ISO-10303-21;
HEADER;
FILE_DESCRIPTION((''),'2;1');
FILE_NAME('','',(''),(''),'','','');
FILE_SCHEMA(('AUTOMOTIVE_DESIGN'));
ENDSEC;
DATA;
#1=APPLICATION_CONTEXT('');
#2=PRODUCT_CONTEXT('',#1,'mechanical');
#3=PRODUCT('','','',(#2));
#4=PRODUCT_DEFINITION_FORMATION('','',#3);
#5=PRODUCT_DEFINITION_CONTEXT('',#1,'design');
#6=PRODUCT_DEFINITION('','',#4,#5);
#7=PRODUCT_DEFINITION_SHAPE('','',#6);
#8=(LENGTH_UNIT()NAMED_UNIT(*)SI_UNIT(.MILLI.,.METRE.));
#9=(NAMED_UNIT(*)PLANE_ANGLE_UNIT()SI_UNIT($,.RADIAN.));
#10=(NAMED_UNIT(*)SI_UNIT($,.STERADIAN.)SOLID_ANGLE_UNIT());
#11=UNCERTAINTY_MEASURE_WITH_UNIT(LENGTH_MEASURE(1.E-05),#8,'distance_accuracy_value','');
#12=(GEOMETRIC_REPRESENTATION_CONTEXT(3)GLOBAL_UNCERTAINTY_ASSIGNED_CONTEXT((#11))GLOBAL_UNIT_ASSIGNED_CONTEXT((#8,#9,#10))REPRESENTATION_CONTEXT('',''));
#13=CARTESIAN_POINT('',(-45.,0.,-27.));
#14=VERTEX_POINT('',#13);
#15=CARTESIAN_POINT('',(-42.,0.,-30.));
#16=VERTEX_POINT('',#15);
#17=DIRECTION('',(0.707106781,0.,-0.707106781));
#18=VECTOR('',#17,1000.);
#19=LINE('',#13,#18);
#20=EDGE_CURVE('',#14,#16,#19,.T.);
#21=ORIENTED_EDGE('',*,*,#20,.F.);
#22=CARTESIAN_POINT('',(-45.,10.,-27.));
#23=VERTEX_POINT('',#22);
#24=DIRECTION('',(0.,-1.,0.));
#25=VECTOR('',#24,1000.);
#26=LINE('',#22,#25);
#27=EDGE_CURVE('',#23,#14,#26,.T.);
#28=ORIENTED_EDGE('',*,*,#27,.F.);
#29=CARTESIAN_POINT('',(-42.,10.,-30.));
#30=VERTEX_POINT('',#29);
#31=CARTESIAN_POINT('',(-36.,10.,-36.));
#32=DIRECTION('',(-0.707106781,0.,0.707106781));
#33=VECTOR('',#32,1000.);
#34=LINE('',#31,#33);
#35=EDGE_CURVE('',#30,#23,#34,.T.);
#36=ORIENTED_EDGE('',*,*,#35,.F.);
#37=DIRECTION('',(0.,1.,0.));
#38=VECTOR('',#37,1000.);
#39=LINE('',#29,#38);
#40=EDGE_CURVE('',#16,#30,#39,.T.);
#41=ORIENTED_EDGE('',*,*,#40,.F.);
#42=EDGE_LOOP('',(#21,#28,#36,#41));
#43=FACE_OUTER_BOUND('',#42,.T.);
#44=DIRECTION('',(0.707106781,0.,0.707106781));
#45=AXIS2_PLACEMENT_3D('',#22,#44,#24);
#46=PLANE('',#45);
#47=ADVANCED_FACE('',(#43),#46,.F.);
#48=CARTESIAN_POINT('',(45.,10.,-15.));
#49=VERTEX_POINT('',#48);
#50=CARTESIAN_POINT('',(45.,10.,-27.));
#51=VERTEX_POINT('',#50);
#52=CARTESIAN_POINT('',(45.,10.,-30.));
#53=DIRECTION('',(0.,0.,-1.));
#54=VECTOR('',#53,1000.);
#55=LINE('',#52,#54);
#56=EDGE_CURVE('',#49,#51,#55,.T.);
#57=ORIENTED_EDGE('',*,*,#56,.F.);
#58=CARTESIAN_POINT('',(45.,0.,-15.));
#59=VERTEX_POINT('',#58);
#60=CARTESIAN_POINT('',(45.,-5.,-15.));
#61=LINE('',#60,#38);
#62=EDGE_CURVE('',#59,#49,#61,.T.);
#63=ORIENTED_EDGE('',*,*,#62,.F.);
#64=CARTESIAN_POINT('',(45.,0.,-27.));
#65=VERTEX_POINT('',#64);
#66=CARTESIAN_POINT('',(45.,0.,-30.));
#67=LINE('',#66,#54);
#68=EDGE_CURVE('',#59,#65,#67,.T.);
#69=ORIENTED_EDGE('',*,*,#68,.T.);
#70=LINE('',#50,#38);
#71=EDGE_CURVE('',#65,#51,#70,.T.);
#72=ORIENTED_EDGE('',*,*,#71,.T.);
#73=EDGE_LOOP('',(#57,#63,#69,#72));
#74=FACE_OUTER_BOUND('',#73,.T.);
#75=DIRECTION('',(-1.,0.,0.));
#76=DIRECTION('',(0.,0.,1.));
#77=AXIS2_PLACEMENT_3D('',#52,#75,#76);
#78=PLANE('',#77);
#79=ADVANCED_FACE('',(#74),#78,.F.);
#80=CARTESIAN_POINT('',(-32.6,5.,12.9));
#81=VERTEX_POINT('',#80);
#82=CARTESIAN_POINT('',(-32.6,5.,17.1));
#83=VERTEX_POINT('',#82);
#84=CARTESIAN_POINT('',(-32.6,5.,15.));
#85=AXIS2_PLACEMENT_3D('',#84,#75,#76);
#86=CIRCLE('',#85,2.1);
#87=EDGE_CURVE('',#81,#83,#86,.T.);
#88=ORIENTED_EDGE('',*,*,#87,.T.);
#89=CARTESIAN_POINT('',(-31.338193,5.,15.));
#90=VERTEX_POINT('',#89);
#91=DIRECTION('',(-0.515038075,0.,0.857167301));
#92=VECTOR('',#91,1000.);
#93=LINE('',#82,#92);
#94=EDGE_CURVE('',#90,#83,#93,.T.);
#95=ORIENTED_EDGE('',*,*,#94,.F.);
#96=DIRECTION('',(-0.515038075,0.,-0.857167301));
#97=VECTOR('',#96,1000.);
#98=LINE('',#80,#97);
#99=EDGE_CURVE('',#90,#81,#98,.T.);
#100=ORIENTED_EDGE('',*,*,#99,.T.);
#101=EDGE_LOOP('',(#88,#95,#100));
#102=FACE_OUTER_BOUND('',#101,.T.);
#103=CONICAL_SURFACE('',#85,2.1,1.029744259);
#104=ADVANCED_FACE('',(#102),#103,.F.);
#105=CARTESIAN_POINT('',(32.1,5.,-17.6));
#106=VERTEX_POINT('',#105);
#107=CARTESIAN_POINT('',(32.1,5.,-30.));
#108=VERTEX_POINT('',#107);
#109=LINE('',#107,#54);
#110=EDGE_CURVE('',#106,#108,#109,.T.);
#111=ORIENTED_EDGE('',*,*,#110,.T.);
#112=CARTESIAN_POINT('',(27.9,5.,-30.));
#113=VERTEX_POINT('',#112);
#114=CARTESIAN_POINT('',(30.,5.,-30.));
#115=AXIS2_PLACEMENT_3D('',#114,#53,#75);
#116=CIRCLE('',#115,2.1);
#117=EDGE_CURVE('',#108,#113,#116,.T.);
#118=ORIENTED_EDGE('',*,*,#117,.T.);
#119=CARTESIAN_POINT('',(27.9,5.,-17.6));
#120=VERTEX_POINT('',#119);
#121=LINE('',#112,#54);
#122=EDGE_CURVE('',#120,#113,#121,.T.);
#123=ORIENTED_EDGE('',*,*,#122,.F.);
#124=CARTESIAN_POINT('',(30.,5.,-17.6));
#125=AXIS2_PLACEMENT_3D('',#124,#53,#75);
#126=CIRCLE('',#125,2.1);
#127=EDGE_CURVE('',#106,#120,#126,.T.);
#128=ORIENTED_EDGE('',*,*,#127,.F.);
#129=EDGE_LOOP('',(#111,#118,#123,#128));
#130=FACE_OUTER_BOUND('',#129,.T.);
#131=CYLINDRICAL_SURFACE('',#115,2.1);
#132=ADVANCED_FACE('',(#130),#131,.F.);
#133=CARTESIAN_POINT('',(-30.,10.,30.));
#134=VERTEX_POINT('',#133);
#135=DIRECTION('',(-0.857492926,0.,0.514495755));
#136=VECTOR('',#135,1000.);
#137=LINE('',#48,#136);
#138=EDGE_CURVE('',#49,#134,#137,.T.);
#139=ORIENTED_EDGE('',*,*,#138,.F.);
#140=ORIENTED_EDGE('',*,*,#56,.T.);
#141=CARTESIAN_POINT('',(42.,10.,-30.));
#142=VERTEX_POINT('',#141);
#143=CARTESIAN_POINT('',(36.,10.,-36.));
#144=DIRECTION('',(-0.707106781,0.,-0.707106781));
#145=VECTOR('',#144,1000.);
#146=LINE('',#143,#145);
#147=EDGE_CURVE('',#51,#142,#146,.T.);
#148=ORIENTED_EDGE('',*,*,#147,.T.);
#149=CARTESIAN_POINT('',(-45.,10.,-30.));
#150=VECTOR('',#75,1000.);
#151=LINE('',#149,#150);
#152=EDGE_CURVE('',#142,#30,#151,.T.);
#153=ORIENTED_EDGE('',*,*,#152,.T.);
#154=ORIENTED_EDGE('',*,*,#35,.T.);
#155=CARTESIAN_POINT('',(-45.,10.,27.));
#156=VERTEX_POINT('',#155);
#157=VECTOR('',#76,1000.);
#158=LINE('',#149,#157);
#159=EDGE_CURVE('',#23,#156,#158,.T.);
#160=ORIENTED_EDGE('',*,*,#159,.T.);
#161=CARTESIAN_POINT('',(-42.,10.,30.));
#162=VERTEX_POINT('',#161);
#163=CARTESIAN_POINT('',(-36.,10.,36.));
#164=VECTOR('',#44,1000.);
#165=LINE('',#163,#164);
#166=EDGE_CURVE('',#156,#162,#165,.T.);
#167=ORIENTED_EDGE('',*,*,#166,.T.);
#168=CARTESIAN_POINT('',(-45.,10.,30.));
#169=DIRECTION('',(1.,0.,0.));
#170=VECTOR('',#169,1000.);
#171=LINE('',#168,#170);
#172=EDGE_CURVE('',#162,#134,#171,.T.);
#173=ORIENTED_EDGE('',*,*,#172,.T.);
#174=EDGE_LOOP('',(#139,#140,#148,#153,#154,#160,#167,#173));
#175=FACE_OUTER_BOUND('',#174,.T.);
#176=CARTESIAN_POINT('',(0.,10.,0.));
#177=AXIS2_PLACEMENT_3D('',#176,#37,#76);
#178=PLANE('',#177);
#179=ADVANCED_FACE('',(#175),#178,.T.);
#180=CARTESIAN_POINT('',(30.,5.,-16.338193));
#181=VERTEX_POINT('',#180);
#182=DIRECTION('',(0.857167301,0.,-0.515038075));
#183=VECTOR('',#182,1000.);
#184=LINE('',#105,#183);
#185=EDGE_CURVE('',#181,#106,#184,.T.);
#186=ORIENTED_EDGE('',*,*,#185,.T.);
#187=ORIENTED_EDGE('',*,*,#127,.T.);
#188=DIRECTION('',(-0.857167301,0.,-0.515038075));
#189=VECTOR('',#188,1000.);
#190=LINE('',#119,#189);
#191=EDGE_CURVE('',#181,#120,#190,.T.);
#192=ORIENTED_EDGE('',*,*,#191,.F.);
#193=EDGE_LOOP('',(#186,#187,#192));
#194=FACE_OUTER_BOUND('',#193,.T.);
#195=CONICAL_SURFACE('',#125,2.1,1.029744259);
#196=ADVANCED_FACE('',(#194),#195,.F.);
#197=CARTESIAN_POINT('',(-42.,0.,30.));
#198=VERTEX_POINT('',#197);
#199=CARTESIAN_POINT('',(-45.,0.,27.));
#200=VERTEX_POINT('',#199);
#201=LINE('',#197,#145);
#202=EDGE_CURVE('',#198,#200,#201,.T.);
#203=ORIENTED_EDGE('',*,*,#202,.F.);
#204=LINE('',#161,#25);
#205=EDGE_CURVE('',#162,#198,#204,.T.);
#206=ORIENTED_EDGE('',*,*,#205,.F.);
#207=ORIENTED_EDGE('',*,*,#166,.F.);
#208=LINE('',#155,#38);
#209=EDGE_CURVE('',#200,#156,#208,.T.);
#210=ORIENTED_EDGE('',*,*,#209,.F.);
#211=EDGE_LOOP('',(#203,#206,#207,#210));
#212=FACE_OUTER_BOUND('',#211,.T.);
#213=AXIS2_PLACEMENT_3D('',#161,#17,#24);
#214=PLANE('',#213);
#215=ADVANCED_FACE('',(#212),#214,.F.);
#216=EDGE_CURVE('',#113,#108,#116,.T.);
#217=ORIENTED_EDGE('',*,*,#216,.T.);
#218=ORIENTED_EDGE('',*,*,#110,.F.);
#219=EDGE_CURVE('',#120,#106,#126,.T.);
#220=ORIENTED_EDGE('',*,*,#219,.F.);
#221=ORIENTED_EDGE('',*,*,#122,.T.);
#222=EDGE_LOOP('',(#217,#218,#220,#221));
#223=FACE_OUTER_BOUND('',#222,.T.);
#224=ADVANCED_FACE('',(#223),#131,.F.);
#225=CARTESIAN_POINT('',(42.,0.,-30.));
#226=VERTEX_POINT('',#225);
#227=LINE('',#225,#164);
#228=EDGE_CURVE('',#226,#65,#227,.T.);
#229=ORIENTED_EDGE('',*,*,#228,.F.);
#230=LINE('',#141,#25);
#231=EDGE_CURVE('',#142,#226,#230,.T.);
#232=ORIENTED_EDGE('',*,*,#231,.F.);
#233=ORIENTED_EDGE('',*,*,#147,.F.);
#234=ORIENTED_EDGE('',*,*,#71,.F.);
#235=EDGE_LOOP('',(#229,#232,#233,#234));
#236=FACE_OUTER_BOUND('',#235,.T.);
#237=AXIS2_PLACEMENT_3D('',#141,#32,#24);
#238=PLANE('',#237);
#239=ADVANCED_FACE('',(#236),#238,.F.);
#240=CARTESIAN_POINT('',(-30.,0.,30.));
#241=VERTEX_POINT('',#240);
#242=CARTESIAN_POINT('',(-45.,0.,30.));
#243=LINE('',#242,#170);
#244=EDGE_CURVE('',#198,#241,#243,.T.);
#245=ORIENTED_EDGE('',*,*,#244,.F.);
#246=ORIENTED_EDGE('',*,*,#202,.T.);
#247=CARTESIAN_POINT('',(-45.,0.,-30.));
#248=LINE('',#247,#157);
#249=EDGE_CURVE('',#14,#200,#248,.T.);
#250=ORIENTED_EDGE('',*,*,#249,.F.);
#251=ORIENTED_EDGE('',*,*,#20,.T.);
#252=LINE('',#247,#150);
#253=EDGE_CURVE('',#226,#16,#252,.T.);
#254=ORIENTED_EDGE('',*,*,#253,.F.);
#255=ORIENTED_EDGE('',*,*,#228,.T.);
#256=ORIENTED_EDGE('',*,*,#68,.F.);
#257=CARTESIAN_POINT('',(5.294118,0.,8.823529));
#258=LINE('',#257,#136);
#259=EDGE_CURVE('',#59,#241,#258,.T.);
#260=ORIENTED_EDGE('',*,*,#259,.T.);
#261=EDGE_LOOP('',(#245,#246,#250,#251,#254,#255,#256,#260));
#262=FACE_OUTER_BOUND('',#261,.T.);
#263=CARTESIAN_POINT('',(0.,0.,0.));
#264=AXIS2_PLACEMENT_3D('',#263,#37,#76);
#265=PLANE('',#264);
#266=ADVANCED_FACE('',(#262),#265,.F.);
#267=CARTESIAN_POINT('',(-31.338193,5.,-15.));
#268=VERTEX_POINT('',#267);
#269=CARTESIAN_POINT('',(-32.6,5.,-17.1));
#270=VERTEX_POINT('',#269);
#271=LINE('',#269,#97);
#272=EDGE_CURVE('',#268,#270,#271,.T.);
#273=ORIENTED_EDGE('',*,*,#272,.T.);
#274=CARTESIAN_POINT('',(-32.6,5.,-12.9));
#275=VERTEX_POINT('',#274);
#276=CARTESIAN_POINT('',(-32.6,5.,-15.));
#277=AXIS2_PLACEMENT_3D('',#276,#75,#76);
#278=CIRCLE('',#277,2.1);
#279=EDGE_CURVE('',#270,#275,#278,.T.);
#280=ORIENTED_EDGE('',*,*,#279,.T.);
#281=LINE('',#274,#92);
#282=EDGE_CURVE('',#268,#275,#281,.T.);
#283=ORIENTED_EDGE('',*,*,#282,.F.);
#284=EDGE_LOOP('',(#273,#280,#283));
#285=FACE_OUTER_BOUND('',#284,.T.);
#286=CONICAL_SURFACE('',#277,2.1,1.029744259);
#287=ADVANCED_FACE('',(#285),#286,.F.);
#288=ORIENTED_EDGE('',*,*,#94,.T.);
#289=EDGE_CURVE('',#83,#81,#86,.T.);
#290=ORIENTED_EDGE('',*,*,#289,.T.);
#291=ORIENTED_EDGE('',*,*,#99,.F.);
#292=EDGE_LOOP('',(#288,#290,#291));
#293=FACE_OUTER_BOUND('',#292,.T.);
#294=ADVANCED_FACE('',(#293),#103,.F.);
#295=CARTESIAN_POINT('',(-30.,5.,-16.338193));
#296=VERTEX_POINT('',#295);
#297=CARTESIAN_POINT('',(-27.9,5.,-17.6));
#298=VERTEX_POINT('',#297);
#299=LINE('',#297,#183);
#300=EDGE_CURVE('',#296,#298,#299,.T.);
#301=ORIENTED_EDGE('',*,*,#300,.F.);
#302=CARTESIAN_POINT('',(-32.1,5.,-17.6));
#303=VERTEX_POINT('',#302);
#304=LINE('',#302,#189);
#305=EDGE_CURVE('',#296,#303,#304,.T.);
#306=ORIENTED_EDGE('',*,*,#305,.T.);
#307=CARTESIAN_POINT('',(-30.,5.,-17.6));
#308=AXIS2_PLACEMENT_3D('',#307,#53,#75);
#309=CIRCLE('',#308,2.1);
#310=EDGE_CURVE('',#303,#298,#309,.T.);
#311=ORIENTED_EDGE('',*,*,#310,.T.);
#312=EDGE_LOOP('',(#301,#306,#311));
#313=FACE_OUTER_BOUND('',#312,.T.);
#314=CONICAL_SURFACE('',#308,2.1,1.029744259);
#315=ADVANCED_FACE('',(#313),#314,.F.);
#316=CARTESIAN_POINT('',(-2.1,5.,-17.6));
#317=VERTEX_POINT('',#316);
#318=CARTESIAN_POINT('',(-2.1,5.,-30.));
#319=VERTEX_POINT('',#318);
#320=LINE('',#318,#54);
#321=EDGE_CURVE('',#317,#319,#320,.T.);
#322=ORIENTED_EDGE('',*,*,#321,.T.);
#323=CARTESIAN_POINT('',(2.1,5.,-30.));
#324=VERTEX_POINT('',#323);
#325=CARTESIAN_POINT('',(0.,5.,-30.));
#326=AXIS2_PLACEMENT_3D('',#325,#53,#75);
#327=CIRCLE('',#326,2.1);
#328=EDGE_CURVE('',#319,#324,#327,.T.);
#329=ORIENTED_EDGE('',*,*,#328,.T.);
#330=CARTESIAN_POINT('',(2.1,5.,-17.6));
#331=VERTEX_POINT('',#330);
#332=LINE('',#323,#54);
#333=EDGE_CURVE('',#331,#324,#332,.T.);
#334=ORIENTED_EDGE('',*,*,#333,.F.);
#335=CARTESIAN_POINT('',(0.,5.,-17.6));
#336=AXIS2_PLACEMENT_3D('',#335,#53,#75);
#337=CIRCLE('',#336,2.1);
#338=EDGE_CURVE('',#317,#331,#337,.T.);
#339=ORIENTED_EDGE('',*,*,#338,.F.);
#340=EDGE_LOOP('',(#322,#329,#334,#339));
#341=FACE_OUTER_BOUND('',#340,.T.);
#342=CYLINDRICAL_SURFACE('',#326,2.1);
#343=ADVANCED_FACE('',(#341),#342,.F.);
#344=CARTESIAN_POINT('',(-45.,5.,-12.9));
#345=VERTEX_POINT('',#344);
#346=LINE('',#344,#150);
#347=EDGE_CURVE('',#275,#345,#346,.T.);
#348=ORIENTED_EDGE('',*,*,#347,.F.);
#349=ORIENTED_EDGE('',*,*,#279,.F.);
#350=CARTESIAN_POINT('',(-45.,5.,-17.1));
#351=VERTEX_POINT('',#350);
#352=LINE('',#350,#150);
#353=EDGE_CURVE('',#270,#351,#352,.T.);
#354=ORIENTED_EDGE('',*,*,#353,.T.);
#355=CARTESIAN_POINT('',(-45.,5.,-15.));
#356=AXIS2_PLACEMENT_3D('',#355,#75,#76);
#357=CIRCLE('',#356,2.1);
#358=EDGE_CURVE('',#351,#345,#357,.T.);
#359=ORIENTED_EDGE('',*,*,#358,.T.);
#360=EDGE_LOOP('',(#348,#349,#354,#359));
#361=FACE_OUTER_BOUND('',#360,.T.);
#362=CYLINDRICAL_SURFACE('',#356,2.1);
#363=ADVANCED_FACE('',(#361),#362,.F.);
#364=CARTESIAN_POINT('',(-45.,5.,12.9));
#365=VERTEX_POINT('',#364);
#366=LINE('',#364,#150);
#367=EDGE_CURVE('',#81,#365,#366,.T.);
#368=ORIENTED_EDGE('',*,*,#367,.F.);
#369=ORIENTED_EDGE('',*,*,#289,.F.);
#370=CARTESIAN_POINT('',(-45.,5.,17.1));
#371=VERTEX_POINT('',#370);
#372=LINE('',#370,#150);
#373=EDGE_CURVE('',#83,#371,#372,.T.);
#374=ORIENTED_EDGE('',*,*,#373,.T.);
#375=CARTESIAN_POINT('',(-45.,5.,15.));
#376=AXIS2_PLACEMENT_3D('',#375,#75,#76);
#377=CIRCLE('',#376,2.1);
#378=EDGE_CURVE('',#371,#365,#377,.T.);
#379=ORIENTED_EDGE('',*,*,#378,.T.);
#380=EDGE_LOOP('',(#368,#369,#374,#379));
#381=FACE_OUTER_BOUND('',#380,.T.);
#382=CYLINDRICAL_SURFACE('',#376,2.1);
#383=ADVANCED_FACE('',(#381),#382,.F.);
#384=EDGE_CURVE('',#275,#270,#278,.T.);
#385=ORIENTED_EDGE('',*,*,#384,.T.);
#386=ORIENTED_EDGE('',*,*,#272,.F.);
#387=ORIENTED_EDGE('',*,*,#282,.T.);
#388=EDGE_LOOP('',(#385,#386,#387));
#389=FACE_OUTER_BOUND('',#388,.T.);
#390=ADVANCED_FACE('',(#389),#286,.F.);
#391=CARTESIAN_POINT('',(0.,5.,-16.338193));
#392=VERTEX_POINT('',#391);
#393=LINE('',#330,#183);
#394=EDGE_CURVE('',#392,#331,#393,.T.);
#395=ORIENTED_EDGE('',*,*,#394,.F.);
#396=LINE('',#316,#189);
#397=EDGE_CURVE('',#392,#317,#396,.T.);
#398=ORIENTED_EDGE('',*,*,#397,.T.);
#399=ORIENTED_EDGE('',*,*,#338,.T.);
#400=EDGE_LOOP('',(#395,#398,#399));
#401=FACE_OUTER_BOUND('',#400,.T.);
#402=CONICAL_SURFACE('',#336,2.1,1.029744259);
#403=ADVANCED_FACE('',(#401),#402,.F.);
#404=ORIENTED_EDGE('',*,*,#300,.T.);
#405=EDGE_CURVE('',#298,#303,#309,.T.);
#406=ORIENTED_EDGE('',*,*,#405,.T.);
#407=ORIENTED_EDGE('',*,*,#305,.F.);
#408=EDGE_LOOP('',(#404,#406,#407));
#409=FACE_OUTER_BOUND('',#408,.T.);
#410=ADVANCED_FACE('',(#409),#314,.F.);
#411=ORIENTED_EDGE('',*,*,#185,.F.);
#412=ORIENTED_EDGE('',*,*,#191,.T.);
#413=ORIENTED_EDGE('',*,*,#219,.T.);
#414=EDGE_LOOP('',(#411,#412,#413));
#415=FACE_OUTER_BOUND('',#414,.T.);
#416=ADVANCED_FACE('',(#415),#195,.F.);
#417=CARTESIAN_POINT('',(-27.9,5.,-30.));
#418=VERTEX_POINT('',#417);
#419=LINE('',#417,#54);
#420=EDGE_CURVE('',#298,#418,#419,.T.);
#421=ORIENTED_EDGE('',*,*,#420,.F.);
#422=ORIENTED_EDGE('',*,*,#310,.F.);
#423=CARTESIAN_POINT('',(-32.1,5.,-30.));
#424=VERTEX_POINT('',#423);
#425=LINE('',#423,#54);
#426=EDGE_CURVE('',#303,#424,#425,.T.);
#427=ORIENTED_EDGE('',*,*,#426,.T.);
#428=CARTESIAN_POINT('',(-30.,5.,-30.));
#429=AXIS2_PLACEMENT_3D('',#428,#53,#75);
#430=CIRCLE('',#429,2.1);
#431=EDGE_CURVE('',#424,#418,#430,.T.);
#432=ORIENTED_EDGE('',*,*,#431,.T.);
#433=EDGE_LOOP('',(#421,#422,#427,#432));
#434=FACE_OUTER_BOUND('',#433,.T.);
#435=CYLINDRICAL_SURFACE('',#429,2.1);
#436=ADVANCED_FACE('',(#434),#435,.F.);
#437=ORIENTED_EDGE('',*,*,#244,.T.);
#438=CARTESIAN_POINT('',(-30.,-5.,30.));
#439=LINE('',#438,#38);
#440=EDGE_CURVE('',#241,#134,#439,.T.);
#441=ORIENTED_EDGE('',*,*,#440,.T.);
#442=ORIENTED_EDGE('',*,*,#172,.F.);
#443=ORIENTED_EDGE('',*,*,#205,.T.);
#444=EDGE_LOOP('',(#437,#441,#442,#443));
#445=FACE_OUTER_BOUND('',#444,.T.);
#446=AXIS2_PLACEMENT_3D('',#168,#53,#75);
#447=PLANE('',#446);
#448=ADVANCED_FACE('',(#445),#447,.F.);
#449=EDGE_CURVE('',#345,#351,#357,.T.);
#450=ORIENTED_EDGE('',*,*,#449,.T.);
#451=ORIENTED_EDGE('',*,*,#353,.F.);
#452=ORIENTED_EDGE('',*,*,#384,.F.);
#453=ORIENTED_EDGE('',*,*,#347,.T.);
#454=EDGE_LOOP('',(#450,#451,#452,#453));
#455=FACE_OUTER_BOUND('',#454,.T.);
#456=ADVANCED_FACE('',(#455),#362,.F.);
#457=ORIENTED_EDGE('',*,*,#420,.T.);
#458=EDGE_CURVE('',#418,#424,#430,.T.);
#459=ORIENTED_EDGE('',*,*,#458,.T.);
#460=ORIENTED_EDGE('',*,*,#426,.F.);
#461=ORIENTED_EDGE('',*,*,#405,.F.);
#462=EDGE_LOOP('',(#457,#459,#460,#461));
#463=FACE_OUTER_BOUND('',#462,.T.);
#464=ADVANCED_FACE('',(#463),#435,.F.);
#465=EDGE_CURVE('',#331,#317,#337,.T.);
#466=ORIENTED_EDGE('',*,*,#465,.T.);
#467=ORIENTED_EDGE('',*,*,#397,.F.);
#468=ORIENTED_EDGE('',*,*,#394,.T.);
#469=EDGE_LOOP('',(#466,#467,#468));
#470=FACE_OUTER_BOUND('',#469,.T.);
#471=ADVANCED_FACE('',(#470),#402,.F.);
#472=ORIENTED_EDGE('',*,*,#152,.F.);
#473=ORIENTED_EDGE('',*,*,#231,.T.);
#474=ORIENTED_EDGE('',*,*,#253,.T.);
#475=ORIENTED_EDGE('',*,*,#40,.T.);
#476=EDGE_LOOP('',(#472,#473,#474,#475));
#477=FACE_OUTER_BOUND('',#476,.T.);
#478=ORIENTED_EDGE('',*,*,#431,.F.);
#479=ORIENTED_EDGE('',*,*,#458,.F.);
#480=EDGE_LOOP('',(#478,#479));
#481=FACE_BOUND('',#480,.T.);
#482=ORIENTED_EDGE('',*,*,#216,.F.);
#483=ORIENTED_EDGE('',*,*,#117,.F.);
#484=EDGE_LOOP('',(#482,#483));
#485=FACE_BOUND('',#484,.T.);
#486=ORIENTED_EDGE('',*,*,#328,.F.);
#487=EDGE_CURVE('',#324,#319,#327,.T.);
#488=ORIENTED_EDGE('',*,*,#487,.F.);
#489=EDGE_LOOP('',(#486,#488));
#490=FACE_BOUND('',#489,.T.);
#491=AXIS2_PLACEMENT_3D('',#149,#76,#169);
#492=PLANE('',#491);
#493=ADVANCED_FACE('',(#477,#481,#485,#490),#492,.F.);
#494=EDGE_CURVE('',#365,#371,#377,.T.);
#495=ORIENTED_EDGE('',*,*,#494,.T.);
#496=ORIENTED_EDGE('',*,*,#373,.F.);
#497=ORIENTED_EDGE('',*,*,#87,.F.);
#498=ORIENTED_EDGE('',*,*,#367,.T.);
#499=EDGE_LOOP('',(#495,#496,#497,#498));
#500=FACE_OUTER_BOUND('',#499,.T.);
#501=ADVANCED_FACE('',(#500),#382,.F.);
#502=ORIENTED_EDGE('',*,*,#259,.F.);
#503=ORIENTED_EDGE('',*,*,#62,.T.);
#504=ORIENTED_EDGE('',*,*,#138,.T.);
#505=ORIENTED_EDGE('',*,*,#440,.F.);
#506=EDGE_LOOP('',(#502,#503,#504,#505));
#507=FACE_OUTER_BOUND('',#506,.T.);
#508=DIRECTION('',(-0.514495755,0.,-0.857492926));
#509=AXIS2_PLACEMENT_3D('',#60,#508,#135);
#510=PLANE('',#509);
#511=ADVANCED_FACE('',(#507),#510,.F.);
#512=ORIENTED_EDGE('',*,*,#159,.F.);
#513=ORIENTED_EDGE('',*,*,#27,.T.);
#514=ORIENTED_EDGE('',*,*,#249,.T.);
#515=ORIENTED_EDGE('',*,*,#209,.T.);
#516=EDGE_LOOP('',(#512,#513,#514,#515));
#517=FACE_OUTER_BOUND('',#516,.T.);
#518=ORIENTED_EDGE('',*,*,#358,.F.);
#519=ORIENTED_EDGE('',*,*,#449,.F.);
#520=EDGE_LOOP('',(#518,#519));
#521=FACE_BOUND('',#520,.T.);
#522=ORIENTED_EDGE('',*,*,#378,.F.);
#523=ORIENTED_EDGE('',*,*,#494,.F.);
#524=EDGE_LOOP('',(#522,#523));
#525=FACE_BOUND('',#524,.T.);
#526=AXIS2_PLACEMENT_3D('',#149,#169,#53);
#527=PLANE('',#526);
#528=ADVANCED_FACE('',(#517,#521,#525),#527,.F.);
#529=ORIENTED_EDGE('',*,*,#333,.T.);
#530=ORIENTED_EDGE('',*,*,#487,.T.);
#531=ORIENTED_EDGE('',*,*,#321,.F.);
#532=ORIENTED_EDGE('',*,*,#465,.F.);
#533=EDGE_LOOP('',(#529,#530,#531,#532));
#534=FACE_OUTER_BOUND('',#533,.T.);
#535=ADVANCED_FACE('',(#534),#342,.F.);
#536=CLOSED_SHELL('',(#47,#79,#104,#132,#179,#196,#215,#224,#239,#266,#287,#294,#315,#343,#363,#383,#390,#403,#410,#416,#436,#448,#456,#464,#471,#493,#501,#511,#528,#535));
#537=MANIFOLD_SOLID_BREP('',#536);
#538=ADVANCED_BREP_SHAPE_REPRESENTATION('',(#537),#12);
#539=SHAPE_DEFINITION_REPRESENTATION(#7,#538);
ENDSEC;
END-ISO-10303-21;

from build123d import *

# Parameters (mm, degrees)
SKETCH_1_W             = 90
SKETCH_1_H             = 60
EXTRUDE_1_DEPTH        = 10
CUT_EXTRUDE_1_DEPTH    = 15
CHAMFER_1_SIZE         = 3
HOLE_WIZARD_M5_1_D     = 4.2
HOLE_WIZARD_M5_1_DEPTH = 12.4
HOLE_WIZARD_M5_1_TIP   = 1.2618073
HOLE_WIZARD_M5_2_D     = 4.2
HOLE_WIZARD_M5_2_DEPTH = 12.4
HOLE_WIZARD_M5_2_TIP   = 1.2618073


with BuildPart() as part:
    # 草图1 → 凸台-拉伸1 (new body)
    with BuildSketch(Plane(origin=(0, 0, 0), x_dir=(1, 0, 0), z_dir=(0, 1, 0))):
        Rectangle(SKETCH_1_W, SKETCH_1_H)
    extrude(amount=EXTRUDE_1_DEPTH)

    # 草图2 → 切除-拉伸1 (cut)
    with BuildSketch(Plane(origin=(0, 10, 0), x_dir=(1, 0, 0), z_dir=(0, 1, 0))):
        Polygon((45, 15), (-30, -30), (45, -30), align=None)
    extrude(amount=-CUT_EXTRUDE_1_DEPTH, mode=Mode.SUBTRACT)

    # 倒角1
    chamfer_1_edges = [part.edges().sort_by_distance(p)[0] for p in [
        (-45, 5, 30),
        (-45, 5, -30),
        (45, 5, -30),
    ]]
    chamfer(chamfer_1_edges, length=CHAMFER_1_SIZE)

    # M5 螺纹孔1
    with Locations(Plane.ZY.offset(45)):
        with Locations((-15, 5), (15, 5)):
            Hole(HOLE_WIZARD_M5_1_D / 2, depth=HOLE_WIZARD_M5_1_DEPTH)
            with Locations((0, 0, -(HOLE_WIZARD_M5_1_DEPTH + HOLE_WIZARD_M5_1_TIP / 2))):  # 118° drill point
                Cone(0, HOLE_WIZARD_M5_1_D / 2, HOLE_WIZARD_M5_1_TIP, mode=Mode.SUBTRACT)

    # M5 螺纹孔2
    with Locations(Plane(origin=(0, 0, -30), x_dir=(-1, 0, 0), z_dir=(0, 0, -1))):
        with Locations((30, 5), (0, 5), (-30, 5)):
            Hole(HOLE_WIZARD_M5_2_D / 2, depth=HOLE_WIZARD_M5_2_DEPTH)
            with Locations((0, 0, -(HOLE_WIZARD_M5_2_DEPTH + HOLE_WIZARD_M5_2_TIP / 2))):  # 118° drill point
                Cone(0, HOLE_WIZARD_M5_2_D / 2, HOLE_WIZARD_M5_2_TIP, mode=Mode.SUBTRACT)


solid = part.part
